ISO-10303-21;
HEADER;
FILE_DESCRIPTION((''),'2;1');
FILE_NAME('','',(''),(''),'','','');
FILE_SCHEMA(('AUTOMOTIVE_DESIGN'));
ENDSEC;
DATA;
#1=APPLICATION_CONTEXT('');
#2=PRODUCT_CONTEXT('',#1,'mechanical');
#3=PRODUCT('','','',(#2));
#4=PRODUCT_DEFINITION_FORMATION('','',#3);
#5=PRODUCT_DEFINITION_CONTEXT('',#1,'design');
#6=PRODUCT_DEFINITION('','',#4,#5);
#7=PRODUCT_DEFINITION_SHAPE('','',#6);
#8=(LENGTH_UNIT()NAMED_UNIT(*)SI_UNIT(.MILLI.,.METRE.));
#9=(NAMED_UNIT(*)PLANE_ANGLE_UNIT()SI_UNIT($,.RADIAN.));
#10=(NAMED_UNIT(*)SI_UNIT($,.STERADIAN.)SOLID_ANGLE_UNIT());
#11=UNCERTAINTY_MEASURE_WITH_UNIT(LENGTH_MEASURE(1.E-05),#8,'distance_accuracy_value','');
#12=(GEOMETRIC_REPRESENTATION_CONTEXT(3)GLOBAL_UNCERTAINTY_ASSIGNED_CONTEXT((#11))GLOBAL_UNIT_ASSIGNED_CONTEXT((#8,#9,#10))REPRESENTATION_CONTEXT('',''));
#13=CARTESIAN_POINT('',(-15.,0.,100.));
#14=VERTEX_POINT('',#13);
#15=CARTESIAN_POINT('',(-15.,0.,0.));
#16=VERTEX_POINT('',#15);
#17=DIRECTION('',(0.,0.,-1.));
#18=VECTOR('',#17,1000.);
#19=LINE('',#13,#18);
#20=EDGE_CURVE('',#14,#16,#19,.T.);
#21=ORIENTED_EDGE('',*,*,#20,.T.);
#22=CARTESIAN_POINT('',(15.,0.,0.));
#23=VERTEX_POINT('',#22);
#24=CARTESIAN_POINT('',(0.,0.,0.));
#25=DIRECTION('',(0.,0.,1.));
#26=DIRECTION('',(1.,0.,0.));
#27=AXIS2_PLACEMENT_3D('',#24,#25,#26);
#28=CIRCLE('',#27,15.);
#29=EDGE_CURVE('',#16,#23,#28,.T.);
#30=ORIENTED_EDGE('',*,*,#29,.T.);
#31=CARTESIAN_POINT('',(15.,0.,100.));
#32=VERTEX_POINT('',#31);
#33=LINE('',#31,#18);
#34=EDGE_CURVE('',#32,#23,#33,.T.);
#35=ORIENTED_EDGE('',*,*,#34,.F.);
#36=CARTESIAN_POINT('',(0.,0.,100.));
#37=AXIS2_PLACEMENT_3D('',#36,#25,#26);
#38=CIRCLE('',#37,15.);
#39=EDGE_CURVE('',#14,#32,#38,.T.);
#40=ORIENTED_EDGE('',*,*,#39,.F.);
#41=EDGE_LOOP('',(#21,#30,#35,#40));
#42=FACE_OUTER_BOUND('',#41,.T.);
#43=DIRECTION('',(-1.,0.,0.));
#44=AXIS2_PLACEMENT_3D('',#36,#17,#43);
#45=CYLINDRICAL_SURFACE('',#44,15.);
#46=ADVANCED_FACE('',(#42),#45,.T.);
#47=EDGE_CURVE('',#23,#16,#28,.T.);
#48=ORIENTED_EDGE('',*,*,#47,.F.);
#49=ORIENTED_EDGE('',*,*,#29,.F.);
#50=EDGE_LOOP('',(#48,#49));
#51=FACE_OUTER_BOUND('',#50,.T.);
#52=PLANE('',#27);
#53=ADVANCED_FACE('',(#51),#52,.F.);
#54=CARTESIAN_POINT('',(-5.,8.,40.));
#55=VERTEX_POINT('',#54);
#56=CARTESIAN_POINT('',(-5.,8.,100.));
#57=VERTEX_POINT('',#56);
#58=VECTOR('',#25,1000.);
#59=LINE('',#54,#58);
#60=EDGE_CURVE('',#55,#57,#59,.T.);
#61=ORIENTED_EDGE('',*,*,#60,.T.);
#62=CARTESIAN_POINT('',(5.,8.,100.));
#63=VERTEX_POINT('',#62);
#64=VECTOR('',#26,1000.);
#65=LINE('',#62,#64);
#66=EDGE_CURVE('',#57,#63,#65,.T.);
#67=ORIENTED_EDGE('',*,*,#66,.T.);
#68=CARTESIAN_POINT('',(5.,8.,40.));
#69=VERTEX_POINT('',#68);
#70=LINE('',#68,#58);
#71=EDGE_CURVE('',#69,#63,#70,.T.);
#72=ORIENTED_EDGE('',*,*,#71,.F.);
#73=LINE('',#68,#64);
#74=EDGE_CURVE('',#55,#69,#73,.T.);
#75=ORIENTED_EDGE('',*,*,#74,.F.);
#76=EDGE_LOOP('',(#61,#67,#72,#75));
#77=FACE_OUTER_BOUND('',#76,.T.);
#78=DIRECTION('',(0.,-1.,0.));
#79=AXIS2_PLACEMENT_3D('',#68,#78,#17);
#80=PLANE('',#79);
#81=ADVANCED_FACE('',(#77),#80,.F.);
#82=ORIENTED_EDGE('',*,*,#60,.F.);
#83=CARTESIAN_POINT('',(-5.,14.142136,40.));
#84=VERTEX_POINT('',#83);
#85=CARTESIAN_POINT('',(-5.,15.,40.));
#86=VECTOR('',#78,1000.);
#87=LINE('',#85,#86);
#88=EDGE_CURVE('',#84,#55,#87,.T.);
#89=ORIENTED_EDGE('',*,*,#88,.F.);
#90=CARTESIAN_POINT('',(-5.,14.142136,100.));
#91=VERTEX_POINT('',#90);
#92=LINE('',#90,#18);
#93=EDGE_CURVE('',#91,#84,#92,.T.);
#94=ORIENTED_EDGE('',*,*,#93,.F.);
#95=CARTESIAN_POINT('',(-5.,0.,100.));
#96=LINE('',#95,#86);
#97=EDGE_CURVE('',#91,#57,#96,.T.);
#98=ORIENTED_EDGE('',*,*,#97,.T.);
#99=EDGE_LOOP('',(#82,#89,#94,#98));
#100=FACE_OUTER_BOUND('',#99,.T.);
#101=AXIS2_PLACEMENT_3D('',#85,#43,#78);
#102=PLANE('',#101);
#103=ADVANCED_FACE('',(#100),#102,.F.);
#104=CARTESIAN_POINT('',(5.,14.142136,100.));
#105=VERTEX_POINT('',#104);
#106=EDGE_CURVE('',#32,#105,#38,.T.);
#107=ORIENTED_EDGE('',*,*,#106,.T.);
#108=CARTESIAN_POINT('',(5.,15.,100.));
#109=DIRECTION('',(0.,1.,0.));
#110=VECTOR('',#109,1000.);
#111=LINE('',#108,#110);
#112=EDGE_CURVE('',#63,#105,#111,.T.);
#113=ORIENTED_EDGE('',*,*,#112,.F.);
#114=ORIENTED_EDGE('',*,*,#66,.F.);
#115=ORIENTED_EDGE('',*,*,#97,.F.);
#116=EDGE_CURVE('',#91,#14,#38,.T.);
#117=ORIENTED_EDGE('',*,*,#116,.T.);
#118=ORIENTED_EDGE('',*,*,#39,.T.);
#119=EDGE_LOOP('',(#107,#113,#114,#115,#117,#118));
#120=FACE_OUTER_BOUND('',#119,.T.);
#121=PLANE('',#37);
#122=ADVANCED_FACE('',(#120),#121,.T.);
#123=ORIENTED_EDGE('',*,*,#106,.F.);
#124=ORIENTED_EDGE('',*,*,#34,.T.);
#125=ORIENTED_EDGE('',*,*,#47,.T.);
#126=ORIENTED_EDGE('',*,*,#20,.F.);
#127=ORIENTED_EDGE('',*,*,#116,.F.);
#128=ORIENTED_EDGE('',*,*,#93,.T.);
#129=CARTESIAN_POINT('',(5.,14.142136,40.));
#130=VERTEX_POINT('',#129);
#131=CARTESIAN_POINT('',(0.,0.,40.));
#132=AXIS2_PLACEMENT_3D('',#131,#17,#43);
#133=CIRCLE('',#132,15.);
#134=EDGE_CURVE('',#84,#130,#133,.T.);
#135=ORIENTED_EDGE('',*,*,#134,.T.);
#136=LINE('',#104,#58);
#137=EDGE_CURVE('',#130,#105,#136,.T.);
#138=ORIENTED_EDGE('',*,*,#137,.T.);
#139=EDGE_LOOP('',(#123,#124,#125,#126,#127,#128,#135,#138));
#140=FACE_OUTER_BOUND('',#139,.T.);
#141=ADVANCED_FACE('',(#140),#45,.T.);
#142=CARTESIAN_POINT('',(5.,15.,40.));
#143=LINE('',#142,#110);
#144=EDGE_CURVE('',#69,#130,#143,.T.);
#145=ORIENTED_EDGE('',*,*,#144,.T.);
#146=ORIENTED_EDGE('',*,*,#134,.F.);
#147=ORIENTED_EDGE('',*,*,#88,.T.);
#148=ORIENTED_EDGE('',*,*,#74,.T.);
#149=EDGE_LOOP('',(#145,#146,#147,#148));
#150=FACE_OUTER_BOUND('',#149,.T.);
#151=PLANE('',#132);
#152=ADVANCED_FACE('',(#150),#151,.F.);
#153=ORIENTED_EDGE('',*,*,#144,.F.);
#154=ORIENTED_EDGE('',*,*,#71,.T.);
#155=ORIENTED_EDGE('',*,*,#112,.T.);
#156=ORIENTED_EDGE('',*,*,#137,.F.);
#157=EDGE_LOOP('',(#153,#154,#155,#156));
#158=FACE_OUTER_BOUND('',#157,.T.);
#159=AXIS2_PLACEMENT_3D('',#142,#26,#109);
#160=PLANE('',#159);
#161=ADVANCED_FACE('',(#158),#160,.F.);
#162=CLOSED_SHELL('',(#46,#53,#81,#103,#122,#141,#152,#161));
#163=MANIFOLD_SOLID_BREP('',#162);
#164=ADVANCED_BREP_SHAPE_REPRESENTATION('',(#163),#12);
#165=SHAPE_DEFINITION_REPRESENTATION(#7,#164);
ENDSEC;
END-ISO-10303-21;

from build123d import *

# Parameters (mm, degrees)
SHAFT_PROFILE_30_R      = 15
SHAFT_BODY_30X100_DEPTH = 100
KEYWAY_PROFILE_W        = 10
KEYWAY_PROFILE_H        = 7
KEYWAY_CUT_60MM_DEPTH   = 60


with BuildPart() as part:
    # Shaft Profile Ø30 → Shaft Body Ø30x100 (new body)
    with BuildSketch(Plane.XY):
        Circle(SHAFT_PROFILE_30_R)
    extrude(amount=SHAFT_BODY_30X100_DEPTH)

    # Keyway Profile → Keyway Cut 60mm (cut)
    with BuildSketch(Plane.XY.offset(100)):
        with Locations((0, 11.5)):
            Rectangle(KEYWAY_PROFILE_W, KEYWAY_PROFILE_H)
    extrude(amount=-KEYWAY_CUT_60MM_DEPTH, mode=Mode.SUBTRACT)


solid = part.part
